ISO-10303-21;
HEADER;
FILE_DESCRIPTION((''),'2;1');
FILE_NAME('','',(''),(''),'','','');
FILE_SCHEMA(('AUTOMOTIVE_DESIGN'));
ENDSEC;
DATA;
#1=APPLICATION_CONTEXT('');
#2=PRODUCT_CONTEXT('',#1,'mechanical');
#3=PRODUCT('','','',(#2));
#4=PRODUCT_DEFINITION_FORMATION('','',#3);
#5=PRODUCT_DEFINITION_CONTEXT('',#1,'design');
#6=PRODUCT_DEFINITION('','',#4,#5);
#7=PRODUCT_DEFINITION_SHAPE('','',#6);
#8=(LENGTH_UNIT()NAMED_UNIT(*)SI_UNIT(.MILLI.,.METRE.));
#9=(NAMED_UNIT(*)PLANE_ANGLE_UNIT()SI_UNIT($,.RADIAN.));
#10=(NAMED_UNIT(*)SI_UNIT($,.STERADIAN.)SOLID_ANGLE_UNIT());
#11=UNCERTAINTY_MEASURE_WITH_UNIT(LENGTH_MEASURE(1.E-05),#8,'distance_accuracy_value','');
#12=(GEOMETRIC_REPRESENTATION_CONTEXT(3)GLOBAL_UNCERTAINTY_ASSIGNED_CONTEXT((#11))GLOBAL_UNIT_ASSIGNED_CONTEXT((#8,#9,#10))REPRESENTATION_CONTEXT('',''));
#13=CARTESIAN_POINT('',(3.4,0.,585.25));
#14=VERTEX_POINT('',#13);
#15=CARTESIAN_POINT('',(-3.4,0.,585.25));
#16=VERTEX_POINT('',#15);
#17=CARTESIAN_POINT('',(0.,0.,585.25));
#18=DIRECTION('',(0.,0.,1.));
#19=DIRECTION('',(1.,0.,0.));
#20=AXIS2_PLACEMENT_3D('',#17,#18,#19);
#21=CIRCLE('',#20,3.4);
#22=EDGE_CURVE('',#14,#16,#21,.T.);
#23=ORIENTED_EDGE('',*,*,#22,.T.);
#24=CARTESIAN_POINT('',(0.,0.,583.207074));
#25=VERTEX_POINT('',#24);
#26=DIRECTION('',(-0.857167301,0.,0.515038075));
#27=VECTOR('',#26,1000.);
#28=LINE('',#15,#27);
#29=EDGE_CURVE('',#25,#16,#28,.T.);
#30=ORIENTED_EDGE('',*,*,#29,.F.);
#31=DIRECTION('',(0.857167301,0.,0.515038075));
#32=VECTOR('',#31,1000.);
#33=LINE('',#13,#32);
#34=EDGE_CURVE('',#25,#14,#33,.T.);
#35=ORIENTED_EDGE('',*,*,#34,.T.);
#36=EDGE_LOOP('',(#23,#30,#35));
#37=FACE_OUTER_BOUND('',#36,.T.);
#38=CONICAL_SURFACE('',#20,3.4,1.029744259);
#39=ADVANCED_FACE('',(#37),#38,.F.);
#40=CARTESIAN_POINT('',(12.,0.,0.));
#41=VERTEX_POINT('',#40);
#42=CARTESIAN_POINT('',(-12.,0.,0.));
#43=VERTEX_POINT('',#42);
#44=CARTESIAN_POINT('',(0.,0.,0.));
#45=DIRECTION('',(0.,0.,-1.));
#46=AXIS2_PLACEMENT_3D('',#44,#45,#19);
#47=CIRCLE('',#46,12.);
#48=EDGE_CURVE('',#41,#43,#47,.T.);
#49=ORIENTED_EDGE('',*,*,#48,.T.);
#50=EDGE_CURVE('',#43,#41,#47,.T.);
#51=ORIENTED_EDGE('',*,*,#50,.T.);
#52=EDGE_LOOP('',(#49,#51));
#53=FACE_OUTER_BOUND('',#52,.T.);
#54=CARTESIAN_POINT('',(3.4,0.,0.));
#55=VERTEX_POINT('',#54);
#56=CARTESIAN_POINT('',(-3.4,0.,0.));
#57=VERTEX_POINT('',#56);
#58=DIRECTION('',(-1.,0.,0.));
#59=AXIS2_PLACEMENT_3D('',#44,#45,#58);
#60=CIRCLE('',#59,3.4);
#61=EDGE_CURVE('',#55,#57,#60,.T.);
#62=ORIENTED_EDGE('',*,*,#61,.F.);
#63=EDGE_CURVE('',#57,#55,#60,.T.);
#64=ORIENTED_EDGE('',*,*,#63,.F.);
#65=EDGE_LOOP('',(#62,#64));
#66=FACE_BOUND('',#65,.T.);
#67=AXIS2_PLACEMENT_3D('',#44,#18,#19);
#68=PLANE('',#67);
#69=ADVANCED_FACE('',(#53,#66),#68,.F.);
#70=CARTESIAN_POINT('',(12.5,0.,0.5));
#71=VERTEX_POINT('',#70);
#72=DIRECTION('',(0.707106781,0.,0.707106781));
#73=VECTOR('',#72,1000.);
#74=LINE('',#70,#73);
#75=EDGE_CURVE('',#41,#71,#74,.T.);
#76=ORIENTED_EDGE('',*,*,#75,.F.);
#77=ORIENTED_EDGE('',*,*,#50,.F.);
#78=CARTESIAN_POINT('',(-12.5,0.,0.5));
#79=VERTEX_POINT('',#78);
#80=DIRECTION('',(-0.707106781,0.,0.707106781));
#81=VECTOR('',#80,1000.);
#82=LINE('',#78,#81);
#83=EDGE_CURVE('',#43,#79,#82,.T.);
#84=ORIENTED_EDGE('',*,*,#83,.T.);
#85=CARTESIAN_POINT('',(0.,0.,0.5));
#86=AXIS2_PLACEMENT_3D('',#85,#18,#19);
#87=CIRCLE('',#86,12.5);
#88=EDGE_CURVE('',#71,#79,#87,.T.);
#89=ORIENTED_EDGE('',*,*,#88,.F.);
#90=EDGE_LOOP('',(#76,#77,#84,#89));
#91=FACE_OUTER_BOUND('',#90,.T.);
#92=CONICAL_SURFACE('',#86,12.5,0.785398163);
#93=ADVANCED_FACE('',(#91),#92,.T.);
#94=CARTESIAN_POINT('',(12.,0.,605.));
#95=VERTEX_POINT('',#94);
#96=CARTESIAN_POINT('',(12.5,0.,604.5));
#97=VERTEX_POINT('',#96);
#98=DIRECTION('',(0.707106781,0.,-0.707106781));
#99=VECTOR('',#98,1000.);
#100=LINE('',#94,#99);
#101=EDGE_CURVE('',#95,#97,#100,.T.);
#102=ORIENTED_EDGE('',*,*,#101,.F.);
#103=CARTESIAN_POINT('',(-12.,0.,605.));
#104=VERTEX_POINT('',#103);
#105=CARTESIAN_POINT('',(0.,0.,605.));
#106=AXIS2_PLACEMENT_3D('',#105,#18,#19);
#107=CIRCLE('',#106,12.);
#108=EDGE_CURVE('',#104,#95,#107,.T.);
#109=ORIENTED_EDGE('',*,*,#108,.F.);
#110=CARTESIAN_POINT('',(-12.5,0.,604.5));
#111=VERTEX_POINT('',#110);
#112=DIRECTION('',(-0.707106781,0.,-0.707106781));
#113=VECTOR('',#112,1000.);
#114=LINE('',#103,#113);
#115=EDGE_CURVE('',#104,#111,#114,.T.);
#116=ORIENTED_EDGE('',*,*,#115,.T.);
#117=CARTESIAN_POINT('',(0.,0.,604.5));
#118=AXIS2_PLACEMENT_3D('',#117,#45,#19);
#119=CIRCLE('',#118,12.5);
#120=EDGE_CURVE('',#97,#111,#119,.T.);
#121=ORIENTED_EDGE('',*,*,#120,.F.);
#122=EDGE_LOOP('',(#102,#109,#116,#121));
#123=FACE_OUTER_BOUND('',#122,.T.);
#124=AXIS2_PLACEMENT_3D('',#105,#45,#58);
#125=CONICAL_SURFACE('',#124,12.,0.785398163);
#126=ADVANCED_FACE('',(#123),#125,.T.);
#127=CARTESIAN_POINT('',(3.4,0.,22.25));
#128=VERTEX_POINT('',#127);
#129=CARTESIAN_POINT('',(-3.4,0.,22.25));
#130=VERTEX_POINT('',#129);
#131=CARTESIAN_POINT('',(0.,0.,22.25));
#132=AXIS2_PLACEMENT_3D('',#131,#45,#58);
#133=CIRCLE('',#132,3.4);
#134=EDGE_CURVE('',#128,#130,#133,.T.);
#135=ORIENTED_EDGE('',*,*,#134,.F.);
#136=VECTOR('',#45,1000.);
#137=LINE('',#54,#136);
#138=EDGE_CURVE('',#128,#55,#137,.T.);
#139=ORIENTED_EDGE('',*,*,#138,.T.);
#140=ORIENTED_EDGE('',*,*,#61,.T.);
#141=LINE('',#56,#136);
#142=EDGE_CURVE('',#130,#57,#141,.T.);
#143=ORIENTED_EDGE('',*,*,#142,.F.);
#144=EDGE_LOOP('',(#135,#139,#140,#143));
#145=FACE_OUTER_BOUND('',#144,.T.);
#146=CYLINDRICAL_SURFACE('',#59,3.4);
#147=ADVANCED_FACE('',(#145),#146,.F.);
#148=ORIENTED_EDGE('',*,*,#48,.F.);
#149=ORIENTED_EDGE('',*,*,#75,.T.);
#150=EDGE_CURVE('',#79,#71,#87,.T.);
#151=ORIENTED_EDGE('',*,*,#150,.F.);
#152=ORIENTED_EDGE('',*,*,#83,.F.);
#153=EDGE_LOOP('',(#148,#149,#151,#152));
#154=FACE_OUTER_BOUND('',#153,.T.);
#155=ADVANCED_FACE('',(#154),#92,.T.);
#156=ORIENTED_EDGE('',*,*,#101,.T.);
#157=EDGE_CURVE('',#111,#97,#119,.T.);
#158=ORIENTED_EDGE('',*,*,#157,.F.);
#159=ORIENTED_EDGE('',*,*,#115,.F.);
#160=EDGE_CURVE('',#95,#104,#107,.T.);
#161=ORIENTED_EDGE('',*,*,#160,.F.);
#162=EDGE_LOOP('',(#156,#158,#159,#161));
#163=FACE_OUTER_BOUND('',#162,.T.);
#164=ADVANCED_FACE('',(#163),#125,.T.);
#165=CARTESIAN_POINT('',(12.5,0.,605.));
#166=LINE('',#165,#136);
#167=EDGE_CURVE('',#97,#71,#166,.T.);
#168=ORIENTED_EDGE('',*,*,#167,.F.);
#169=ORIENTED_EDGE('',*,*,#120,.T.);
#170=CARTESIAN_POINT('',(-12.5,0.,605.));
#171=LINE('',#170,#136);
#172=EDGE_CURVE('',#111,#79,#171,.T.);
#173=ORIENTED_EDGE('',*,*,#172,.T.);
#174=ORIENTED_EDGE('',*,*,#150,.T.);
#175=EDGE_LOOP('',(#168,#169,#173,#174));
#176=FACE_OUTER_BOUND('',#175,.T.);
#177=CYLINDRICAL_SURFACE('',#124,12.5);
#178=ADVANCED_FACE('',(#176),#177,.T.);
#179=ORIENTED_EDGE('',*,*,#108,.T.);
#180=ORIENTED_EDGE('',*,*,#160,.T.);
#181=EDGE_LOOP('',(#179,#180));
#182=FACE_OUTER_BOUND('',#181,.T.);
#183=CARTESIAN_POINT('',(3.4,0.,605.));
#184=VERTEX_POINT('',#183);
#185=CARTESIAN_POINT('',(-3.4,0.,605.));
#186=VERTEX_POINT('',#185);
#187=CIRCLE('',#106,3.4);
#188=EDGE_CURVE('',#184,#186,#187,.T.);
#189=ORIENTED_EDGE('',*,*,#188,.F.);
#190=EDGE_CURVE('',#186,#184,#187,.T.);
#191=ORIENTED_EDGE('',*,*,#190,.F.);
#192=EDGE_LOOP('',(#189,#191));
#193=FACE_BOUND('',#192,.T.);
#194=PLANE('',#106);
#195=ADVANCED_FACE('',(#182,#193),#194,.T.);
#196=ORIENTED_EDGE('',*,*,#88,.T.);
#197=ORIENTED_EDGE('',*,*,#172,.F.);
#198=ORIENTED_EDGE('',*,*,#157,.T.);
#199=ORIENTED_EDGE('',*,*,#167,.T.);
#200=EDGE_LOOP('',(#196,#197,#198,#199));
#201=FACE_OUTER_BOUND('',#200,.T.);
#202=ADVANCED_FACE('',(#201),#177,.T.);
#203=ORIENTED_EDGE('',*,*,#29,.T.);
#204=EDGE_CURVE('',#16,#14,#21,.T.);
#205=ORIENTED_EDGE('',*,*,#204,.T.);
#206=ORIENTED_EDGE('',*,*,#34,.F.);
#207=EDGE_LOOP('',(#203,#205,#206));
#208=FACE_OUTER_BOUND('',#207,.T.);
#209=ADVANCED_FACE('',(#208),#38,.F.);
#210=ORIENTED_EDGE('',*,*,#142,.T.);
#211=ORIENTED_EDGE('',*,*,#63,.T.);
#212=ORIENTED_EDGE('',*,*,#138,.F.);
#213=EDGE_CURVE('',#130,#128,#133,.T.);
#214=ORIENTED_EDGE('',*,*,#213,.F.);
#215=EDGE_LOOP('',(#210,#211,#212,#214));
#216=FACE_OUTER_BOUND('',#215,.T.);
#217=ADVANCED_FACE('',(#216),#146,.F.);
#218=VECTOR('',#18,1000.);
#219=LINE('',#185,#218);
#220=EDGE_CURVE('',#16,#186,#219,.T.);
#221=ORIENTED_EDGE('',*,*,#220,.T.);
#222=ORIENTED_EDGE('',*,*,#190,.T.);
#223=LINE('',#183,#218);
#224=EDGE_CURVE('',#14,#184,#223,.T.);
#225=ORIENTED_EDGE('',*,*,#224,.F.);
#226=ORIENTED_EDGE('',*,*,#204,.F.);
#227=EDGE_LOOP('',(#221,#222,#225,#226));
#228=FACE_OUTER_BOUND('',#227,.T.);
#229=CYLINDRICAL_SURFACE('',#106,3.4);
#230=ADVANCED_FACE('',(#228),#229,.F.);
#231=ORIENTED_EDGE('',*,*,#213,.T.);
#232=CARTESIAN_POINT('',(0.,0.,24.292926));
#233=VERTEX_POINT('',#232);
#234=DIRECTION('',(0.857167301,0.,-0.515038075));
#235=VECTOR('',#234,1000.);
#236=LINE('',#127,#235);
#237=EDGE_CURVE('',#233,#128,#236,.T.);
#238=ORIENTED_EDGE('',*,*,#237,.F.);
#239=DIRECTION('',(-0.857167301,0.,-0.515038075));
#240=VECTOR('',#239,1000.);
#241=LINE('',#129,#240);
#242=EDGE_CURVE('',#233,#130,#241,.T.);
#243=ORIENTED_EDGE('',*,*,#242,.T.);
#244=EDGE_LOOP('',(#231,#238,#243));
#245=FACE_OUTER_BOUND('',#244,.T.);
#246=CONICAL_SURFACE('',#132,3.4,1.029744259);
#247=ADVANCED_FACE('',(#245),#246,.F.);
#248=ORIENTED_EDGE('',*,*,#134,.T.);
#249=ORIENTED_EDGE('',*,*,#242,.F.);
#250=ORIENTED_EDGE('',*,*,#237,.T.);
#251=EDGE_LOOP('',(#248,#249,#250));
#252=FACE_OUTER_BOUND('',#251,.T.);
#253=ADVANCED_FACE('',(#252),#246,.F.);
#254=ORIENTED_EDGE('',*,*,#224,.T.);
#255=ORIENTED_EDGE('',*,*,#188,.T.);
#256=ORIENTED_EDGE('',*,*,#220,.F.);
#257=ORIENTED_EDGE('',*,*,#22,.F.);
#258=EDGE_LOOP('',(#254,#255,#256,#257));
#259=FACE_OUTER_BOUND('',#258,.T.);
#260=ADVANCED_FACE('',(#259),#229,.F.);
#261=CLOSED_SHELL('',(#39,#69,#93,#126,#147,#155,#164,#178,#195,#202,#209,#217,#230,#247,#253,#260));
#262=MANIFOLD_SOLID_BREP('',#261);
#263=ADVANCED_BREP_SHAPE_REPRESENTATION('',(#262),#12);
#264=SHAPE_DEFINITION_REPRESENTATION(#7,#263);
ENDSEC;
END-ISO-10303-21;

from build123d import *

# Parameters (mm, degrees)
SKETCH_1_R             = 12.5
EXTRUDE_1_DEPTH        = 605
HOLE_WIZARD_M8_1_D     = 6.8
HOLE_WIZARD_M8_1_DEPTH = 22.25
HOLE_WIZARD_M8_1_TIP   = 2.042926105
CHAMFER_1_SIZE         = 0.5
HOLE_WIZARD_M8_2_D     = 6.8
HOLE_WIZARD_M8_2_DEPTH = 19.75
HOLE_WIZARD_M8_2_TIP   = 2.042926105


with BuildPart() as part:
    # 草图1 → 凸台-拉伸1 (new body)
    with BuildSketch(Plane.XY):
        Circle(SKETCH_1_R)
    extrude(amount=EXTRUDE_1_DEPTH)

    # M8 螺纹孔1
    with Locations(Plane(origin=(0, 0, 0), x_dir=(1, 0, 0), z_dir=(0, 0, -1))):
        with Locations((0, 0)):
            Hole(HOLE_WIZARD_M8_1_D / 2, depth=HOLE_WIZARD_M8_1_DEPTH)
            with Locations((0, 0, -(HOLE_WIZARD_M8_1_DEPTH + HOLE_WIZARD_M8_1_TIP / 2))):  # 118° drill point
                Cone(0, HOLE_WIZARD_M8_1_D / 2, HOLE_WIZARD_M8_1_TIP, mode=Mode.SUBTRACT)

    # 倒角1
    chamfer_1_edges = [part.edges().sort_by_distance(p)[0] for p in [
        (-12.5, 0, 0),
        (-12.5, 0, 605),
    ]]
    chamfer(chamfer_1_edges, length=CHAMFER_1_SIZE)

    # M8 螺纹孔2
    with Locations(Plane.XY.offset(605)):
        with Locations((0, 0)):
            Hole(HOLE_WIZARD_M8_2_D / 2, depth=HOLE_WIZARD_M8_2_DEPTH)
            with Locations((0, 0, -(HOLE_WIZARD_M8_2_DEPTH + HOLE_WIZARD_M8_2_TIP / 2))):  # 118° drill point
                Cone(0, HOLE_WIZARD_M8_2_D / 2, HOLE_WIZARD_M8_2_TIP, mode=Mode.SUBTRACT)


solid = part.part
